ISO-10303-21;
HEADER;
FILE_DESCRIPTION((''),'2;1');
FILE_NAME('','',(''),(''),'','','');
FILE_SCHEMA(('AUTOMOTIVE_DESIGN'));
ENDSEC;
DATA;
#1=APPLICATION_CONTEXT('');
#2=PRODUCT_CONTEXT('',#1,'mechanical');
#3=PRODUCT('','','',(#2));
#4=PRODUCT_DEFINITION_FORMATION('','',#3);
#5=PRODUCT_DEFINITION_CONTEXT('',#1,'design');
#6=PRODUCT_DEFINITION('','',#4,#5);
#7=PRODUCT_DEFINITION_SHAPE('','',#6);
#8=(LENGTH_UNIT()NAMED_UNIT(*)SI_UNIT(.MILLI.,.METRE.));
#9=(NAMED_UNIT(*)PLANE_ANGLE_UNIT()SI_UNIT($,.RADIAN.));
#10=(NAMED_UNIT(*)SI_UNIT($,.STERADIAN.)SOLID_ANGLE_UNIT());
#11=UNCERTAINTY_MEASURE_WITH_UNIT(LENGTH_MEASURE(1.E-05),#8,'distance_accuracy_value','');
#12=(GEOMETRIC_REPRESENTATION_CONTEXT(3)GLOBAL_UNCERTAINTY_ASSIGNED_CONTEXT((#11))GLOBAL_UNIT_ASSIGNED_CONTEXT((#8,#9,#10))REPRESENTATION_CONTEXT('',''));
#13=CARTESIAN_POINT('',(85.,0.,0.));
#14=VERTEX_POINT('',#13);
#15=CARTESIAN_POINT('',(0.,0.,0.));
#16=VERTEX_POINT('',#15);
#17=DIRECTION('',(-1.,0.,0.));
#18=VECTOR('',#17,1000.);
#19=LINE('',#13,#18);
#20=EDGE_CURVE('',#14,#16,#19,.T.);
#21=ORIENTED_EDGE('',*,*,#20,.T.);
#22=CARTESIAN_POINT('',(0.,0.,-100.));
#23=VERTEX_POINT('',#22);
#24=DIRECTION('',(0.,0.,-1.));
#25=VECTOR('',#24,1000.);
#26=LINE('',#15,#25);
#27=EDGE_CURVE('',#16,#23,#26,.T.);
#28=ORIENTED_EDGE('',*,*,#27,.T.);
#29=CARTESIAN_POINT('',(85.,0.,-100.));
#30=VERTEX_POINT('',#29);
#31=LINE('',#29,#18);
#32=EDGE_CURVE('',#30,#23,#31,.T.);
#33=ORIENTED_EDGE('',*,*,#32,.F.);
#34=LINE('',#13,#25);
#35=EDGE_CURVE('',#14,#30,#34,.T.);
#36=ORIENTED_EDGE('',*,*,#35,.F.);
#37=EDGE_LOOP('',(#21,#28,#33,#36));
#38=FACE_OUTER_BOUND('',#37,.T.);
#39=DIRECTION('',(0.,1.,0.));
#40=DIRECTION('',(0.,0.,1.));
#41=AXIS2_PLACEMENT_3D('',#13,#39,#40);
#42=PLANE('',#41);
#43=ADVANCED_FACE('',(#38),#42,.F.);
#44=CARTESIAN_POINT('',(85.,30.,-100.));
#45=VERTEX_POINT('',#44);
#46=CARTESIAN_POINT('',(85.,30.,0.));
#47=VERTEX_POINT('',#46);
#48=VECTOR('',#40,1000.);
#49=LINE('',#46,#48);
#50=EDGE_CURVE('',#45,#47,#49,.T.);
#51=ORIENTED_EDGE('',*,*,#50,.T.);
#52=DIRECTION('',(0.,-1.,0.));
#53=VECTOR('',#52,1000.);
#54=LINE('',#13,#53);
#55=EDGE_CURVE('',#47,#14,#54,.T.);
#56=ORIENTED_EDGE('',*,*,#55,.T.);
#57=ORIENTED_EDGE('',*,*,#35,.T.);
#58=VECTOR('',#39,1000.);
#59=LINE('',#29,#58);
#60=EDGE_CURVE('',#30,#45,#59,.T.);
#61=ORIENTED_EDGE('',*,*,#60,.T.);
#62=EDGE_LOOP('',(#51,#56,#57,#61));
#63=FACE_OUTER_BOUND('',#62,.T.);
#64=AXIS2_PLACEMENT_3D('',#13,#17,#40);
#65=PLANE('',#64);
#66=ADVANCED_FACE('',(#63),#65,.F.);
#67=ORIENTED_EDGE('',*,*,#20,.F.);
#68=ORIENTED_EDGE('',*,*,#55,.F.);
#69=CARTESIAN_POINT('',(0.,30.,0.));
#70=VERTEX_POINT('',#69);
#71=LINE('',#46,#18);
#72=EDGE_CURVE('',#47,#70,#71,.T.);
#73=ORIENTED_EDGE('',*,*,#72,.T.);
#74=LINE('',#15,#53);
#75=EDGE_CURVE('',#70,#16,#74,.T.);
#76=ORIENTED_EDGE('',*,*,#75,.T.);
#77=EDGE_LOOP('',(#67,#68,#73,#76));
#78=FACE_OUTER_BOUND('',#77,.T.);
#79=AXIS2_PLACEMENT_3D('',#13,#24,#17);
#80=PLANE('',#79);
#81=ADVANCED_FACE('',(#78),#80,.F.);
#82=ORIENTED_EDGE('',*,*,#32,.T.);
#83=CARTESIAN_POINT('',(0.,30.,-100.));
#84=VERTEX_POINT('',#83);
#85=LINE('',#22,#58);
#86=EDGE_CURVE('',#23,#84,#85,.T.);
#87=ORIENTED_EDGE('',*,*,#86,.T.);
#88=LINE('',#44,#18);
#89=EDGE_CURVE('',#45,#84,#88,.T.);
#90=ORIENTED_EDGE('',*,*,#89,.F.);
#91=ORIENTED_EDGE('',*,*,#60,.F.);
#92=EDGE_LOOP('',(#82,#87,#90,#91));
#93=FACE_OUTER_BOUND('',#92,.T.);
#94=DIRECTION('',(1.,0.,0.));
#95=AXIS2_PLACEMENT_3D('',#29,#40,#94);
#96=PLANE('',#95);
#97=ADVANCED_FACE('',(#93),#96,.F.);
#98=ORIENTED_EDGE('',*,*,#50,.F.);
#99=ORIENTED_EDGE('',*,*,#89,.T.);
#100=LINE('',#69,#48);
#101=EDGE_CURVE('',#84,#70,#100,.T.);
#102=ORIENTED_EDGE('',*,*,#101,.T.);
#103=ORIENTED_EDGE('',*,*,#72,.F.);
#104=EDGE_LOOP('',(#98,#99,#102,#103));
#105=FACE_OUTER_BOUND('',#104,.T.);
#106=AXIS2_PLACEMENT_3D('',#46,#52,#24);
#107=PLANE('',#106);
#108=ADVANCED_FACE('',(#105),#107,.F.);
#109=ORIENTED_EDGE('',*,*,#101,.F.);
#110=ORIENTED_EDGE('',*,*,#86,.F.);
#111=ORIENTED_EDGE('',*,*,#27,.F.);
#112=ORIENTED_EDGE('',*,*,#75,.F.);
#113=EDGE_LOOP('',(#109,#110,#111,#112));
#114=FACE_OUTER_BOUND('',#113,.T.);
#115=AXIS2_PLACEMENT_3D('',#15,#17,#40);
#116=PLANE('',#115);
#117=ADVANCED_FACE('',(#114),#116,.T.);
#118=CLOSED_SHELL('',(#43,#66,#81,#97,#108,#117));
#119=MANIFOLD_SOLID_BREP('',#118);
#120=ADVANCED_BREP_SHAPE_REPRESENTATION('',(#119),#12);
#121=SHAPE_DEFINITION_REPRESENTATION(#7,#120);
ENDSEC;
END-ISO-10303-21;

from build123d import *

# Parameters (mm, degrees)
SKETCH1_W           = 100
SKETCH1_H           = 30
BOSS_EXTRUDE1_DEPTH = 85


with BuildPart() as part:
    # Sketch1 → Boss-Extrude1 (new body)
    with BuildSketch(Plane(origin=(0, 0, 0), x_dir=(0, 0, -1), z_dir=(1, 0, 0))):
        with Locations((50, 15)):
            Rectangle(SKETCH1_W, SKETCH1_H)
    extrude(amount=BOSS_EXTRUDE1_DEPTH)


solid = part.part
